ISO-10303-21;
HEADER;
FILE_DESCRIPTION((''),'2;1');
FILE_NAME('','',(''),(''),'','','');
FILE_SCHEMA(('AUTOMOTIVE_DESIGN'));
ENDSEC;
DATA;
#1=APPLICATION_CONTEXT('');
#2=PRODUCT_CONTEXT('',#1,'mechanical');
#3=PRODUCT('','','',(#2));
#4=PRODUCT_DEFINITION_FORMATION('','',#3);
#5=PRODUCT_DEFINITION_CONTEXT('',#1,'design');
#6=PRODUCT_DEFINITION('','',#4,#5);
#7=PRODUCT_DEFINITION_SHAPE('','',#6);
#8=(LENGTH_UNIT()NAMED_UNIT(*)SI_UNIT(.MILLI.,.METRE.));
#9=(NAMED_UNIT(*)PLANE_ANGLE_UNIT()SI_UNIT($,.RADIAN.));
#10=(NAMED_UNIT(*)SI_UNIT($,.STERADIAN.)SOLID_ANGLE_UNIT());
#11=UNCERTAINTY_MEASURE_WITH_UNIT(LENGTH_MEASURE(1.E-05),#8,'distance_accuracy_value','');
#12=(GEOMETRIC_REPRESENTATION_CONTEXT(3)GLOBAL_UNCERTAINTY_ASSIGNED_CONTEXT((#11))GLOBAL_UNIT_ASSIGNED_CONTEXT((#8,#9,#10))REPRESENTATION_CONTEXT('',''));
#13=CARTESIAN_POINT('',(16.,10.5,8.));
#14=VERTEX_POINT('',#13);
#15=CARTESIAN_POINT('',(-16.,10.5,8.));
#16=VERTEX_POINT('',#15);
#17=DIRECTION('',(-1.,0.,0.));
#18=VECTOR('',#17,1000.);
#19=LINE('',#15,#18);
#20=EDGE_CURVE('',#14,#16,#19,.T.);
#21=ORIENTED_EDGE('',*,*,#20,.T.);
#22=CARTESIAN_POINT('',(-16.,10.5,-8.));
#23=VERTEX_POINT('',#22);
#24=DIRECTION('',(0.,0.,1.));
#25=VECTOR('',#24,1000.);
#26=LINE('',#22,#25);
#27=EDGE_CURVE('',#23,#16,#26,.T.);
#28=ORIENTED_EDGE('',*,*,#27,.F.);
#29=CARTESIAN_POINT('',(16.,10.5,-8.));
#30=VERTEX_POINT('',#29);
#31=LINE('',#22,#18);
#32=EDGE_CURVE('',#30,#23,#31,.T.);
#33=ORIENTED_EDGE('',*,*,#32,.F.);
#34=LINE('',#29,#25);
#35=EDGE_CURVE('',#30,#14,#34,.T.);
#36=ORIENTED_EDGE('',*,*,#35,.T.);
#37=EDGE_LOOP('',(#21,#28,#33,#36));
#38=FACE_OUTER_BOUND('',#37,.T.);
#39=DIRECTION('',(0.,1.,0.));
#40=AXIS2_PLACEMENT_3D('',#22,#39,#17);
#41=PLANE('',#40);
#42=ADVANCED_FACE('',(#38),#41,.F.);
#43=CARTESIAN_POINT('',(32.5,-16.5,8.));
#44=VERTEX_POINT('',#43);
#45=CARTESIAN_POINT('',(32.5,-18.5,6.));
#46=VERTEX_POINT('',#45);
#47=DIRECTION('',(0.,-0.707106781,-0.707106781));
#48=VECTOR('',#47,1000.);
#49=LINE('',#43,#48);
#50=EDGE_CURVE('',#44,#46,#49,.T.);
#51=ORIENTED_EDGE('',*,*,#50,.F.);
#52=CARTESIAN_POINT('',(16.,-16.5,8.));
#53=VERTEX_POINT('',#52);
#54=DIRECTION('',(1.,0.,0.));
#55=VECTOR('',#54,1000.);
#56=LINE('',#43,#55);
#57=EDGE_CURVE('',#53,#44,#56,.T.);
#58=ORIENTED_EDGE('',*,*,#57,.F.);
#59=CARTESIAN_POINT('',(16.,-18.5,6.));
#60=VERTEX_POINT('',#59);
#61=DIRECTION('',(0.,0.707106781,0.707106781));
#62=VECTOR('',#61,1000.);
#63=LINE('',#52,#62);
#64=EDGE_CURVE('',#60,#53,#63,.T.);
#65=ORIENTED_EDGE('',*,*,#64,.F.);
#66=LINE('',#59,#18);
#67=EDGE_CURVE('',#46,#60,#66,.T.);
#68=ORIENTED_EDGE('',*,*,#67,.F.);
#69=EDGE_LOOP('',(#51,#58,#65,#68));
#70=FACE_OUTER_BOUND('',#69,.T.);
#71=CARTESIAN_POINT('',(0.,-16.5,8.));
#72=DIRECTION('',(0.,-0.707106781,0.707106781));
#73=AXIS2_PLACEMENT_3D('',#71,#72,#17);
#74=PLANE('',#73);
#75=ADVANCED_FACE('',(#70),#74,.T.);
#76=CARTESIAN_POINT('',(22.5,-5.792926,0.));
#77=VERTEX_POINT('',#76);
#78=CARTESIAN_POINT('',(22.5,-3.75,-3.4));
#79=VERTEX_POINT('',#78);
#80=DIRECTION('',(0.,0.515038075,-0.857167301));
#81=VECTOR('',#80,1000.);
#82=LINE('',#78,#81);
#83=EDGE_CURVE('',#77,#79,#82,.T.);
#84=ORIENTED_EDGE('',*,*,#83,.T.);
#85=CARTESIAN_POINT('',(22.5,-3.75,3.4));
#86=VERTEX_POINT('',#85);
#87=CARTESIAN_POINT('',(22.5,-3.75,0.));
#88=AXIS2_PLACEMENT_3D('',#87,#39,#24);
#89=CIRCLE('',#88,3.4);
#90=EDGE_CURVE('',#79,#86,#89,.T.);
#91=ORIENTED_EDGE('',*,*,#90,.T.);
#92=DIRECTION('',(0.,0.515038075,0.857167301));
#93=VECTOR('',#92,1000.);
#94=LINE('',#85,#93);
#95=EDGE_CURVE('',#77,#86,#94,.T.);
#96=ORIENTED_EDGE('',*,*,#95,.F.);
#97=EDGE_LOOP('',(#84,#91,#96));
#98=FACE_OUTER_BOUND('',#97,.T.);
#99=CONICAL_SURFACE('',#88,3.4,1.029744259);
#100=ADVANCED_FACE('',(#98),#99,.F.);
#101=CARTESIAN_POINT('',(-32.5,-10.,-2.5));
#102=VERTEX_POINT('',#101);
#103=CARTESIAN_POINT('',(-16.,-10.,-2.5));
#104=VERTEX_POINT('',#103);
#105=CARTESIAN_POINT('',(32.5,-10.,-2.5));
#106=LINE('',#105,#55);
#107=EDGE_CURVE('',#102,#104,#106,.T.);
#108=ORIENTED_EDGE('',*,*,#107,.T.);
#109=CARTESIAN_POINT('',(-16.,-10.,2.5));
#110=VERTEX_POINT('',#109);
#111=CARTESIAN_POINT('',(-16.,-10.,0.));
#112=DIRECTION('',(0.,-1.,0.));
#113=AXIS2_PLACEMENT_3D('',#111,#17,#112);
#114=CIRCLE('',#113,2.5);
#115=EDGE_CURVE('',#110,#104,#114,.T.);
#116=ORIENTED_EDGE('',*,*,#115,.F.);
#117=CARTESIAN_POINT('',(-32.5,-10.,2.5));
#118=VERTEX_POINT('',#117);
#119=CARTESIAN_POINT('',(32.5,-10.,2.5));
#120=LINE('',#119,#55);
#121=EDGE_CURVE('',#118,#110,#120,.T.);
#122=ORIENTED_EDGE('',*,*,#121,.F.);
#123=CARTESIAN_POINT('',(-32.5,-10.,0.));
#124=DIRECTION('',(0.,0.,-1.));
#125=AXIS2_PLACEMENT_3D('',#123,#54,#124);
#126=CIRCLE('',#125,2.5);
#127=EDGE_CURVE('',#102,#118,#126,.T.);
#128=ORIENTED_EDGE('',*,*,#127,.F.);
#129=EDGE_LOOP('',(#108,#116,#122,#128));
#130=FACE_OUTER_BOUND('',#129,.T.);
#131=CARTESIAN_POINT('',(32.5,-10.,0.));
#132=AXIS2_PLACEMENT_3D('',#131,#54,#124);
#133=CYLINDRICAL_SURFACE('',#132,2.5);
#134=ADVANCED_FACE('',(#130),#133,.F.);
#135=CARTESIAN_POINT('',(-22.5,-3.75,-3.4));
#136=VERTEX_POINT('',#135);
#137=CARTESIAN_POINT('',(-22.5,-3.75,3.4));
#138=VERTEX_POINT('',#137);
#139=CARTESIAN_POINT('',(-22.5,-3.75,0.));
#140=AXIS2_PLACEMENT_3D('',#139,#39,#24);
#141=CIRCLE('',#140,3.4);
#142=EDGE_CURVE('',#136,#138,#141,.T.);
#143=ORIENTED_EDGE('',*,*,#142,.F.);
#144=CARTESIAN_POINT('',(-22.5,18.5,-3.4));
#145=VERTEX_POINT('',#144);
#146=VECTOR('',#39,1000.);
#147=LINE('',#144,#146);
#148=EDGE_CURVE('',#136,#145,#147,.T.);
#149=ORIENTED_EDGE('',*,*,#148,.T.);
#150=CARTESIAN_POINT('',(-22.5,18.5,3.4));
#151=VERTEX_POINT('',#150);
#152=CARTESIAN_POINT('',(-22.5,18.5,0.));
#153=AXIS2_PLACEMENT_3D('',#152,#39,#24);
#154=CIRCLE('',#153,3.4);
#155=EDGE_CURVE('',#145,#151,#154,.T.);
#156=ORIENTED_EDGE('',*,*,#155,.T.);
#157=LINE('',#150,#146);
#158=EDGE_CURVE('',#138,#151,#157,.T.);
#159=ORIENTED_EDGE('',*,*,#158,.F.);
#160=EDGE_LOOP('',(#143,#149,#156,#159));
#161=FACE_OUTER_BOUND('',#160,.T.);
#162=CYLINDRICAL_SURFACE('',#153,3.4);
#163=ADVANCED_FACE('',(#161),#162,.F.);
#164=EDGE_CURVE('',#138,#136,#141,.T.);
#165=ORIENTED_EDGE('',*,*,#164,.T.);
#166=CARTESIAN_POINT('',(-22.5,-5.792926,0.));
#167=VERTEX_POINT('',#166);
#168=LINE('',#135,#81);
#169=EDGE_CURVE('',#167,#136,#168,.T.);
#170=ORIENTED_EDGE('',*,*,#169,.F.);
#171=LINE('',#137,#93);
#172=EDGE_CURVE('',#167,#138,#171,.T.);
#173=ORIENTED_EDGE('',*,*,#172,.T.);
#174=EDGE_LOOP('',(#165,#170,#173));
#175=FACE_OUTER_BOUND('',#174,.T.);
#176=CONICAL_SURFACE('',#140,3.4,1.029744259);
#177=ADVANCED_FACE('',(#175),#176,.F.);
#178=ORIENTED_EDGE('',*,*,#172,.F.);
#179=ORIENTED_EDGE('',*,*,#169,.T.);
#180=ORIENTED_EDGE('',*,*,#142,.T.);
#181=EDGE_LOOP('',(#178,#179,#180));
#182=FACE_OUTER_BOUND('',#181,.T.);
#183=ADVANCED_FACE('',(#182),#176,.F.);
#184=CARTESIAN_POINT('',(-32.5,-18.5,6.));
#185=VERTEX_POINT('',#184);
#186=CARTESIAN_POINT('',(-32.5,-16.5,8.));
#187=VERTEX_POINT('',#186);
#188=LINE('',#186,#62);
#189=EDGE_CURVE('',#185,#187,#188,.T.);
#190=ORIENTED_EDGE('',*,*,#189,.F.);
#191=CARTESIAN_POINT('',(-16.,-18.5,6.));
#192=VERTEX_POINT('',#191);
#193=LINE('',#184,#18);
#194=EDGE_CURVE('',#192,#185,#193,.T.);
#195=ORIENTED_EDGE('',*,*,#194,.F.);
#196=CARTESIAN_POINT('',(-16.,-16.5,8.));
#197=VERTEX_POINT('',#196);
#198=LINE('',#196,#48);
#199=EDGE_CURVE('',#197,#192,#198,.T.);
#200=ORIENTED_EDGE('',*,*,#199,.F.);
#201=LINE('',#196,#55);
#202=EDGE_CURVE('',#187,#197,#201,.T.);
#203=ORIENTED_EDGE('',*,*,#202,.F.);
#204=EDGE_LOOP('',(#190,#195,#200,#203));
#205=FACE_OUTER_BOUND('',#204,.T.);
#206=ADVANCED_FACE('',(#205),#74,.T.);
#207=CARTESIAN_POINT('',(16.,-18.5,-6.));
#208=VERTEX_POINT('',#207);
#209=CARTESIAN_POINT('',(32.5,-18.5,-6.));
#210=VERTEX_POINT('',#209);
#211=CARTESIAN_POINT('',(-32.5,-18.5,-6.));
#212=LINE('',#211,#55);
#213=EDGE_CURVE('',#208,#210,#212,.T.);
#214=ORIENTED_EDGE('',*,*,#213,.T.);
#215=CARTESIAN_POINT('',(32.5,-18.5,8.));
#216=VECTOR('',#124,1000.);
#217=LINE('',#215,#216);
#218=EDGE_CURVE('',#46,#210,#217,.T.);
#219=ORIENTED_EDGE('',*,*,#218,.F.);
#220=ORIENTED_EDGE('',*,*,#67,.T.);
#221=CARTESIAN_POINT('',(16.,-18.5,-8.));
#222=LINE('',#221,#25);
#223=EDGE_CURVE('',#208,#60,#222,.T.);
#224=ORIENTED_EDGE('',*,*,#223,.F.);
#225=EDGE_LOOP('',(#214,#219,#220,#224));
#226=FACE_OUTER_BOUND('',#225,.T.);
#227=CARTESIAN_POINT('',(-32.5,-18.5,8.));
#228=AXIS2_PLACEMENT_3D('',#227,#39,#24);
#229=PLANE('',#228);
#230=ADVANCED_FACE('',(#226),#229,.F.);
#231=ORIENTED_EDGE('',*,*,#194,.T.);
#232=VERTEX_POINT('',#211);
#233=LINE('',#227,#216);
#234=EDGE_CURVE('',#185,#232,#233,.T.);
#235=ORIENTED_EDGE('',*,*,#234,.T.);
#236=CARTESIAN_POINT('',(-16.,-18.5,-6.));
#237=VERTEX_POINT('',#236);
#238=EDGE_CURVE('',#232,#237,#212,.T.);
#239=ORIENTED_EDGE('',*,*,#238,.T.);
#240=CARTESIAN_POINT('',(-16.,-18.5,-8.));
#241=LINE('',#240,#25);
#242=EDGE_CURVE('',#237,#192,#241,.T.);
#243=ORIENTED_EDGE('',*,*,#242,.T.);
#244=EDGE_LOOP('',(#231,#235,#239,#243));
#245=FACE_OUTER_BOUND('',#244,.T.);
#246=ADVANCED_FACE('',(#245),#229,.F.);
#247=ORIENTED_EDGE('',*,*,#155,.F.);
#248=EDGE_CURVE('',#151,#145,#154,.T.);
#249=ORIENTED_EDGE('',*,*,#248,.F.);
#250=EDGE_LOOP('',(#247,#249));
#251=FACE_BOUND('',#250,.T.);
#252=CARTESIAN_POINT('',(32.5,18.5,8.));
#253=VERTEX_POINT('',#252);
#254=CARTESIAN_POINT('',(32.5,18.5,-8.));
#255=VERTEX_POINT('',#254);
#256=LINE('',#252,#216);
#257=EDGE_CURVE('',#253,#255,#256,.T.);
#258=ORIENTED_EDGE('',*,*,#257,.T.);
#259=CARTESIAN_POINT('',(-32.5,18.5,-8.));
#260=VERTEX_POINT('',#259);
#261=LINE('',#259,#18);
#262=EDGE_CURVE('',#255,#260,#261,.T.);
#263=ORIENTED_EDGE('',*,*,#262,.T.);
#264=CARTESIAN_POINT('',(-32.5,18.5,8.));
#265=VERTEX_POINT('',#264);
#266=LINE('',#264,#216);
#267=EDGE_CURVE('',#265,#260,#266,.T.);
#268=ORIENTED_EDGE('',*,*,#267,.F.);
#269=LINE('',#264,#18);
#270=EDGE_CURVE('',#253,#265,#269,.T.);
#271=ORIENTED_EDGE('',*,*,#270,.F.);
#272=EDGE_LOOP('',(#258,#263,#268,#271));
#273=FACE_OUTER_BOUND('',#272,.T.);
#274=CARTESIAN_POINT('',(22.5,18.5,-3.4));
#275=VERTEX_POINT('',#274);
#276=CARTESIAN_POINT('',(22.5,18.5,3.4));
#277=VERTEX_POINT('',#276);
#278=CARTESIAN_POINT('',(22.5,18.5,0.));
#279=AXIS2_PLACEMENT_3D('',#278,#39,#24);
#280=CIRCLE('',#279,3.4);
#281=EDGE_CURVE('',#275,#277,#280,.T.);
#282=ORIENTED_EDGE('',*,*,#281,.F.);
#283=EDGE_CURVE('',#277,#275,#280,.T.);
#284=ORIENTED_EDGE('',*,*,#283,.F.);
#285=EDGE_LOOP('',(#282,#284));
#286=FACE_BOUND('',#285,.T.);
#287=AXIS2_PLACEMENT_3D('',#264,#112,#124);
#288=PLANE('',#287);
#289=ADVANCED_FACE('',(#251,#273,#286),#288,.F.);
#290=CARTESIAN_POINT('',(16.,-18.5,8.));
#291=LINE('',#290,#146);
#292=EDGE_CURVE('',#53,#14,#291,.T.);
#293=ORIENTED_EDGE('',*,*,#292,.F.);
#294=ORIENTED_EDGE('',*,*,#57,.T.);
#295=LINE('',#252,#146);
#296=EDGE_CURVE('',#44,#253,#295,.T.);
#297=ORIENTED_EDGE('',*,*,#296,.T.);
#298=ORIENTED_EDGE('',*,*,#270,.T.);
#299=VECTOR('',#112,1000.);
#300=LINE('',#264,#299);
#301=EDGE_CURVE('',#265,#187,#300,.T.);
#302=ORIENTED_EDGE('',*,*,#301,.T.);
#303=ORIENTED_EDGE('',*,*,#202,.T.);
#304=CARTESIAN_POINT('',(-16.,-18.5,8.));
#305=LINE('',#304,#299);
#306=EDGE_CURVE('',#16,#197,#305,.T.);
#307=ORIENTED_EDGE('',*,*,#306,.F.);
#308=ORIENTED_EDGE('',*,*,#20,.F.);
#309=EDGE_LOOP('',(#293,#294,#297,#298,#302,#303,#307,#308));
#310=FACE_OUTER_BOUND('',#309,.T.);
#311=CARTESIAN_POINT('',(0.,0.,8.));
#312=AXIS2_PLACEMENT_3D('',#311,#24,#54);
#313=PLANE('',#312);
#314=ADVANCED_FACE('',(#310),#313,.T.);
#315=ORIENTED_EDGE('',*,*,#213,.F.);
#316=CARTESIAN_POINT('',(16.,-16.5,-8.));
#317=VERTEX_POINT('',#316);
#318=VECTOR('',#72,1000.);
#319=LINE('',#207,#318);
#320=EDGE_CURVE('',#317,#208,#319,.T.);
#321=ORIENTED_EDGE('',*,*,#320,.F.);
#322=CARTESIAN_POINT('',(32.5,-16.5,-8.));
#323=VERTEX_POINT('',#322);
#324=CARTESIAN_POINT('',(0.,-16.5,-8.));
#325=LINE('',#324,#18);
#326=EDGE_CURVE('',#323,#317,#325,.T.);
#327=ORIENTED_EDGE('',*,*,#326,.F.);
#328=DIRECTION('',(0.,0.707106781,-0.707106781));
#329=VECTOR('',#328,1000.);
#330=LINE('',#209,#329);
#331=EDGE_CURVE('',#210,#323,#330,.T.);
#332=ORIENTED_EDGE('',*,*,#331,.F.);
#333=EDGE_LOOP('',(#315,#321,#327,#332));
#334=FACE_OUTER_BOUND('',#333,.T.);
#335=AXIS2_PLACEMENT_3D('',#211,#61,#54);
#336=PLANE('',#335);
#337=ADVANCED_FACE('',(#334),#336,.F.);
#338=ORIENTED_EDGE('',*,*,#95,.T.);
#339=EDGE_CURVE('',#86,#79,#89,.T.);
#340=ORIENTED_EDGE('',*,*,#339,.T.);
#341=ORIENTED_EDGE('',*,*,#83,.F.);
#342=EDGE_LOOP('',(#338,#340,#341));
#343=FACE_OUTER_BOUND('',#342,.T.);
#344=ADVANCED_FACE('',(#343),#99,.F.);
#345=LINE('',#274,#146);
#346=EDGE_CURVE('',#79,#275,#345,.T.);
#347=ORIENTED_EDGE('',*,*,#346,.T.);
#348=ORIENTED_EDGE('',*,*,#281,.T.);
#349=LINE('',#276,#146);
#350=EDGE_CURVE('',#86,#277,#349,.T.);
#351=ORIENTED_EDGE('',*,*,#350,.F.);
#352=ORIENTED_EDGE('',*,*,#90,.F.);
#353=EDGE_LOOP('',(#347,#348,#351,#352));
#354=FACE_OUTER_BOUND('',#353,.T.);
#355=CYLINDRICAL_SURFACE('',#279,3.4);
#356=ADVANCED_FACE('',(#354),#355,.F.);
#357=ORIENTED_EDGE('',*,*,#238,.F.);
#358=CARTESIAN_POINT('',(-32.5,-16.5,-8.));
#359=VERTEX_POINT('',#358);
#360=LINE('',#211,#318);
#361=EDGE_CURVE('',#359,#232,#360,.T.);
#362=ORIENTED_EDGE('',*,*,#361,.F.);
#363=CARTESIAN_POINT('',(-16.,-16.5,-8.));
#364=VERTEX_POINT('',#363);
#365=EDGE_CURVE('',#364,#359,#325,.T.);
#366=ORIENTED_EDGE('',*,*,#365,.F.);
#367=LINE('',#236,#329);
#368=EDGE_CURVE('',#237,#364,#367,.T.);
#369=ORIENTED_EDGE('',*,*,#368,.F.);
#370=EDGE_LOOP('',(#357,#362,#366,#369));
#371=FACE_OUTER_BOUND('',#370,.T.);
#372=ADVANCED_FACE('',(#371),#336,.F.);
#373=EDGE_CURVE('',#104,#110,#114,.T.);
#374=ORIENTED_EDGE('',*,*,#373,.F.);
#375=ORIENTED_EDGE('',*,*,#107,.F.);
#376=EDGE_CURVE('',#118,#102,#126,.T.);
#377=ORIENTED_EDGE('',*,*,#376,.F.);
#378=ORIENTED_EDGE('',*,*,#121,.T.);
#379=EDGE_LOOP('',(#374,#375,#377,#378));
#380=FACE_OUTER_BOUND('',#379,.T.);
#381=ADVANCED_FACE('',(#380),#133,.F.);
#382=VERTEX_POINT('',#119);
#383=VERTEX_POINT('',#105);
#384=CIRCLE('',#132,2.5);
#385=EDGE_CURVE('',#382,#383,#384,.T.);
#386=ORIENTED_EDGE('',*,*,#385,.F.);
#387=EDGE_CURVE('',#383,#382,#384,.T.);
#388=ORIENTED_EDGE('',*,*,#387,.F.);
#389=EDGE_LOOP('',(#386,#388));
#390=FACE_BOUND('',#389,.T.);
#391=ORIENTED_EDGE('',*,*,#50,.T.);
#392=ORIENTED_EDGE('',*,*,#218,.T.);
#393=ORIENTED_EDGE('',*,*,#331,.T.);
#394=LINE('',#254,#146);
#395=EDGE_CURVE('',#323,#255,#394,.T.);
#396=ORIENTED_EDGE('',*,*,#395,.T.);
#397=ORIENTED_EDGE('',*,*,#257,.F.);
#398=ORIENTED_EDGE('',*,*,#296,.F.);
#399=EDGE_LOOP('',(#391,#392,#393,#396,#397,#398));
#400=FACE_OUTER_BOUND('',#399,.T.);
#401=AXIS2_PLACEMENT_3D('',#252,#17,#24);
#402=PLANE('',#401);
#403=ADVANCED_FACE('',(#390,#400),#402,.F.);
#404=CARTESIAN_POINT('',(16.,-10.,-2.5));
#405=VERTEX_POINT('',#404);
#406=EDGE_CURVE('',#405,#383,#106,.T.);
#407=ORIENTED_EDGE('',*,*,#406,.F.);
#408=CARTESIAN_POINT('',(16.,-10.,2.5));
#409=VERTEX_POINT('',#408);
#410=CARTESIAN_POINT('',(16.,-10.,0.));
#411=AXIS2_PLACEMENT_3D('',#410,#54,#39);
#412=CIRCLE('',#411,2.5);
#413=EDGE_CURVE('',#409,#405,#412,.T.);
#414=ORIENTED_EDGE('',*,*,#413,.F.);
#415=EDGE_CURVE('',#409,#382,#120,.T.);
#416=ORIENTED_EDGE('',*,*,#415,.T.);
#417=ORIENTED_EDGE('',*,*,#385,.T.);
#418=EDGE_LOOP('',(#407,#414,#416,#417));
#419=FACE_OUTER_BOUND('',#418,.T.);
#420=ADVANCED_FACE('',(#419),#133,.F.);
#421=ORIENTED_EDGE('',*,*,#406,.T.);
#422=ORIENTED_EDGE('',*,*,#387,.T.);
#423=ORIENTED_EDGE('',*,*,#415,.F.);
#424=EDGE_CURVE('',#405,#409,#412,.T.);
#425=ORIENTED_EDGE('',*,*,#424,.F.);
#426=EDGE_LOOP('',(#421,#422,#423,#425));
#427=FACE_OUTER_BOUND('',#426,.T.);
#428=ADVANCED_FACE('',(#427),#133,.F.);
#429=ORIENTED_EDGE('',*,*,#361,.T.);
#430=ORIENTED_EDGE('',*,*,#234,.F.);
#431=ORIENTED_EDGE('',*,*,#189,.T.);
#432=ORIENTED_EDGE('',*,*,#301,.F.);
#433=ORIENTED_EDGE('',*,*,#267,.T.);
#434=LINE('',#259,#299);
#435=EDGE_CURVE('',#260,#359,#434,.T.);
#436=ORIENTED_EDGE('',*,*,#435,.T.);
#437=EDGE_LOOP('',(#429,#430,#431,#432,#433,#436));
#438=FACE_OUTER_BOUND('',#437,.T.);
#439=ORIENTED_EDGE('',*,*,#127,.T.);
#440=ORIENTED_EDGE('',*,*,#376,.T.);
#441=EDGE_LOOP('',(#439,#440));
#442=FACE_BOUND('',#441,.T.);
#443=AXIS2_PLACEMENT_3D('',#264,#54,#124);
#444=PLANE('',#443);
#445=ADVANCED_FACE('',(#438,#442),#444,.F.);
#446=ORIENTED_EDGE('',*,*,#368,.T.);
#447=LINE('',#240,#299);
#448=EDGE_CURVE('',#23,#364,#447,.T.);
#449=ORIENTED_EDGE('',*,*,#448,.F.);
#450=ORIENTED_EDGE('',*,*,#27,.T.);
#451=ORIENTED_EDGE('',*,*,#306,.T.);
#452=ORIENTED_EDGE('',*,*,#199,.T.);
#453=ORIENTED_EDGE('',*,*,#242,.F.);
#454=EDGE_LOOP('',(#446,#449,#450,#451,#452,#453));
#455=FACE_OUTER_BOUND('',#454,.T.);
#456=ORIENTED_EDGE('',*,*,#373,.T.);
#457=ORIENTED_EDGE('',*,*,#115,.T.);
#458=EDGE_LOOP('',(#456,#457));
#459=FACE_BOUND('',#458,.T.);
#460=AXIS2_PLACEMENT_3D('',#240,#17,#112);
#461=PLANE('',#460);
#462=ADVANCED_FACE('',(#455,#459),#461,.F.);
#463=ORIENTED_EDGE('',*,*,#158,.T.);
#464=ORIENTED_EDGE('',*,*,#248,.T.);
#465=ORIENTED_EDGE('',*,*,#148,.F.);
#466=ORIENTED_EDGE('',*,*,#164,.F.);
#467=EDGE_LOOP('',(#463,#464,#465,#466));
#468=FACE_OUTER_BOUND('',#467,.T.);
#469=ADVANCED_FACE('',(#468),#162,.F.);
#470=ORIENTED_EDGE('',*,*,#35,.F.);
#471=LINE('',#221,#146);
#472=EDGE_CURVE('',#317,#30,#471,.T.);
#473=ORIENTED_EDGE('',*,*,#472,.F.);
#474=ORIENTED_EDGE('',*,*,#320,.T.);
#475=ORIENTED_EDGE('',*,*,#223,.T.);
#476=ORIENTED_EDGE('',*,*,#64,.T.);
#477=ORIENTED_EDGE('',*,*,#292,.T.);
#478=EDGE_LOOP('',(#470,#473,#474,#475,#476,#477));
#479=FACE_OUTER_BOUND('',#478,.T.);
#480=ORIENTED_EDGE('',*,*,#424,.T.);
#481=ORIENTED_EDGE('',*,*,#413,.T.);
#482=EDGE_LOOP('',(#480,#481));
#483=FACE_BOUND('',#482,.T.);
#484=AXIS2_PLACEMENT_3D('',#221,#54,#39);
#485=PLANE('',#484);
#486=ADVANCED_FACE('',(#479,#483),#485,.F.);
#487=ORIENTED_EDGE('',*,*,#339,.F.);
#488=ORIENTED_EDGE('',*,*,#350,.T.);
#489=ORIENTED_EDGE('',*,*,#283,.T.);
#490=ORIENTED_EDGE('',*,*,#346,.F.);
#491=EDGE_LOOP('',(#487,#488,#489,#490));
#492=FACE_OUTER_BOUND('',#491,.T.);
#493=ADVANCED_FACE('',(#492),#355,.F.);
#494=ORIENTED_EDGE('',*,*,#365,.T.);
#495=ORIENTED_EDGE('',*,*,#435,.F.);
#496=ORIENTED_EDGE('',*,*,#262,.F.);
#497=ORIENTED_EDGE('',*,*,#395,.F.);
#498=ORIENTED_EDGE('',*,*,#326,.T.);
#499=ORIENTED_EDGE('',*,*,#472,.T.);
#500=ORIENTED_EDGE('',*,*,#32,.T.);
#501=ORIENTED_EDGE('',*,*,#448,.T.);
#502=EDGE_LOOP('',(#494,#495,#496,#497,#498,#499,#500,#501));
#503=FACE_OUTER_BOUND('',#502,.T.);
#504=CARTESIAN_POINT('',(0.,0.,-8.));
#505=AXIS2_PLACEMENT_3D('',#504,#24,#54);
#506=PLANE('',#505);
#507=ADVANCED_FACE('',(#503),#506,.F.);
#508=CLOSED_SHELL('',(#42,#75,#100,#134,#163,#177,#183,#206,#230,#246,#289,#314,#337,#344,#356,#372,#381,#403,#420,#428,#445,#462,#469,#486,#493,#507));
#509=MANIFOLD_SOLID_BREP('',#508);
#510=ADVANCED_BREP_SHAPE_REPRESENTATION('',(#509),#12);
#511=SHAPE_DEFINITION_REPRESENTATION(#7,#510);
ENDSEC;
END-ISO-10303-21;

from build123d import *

# Parameters (mm, degrees)
SKETCH_1_W             = 65
SKETCH_1_H             = 37
EXTRUDE_1_DEPTH        = 8
SKETCH_3_W             = 32
SKETCH_3_H             = 29
CUT_EXTRUDE_1_DEPTH    = 41.675545479
HOLE_WIZARD_M6_1_D     = 5
HOLE_WIZARD_M8_2_D     = 6.8
HOLE_WIZARD_M8_2_DEPTH = 22.25
HOLE_WIZARD_M8_2_TIP   = 2.042926105
CHAMFER_1_SIZE         = 2


with BuildPart() as part:
    # 草图1 → 凸台-拉伸1 (new, symmetric)
    with BuildSketch(Plane.XY):
        Rectangle(SKETCH_1_W, SKETCH_1_H)
    extrude(amount=EXTRUDE_1_DEPTH, both=True)

    # 草图3 → 切除-拉伸1 (cut, through all)
    with BuildSketch(Plane.XY.offset(8)):
        with Locations((0, -4)):
            Rectangle(SKETCH_3_W, SKETCH_3_H)
    extrude(amount=-CUT_EXTRUDE_1_DEPTH, mode=Mode.SUBTRACT)

    # M6 螺纹孔1 (through all)
    with Locations(Plane(origin=(32.5, 0, 0), x_dir=(0, 0, -1), z_dir=(1, 0, 0))):
        with Locations((0, -10)):
            Hole(HOLE_WIZARD_M6_1_D / 2)

    # M8 螺纹孔2
    with Locations(Plane(origin=(0, 18.5, 0), x_dir=(1, 0, 0), z_dir=(0, 1, 0))):
        with Locations((-22.5, 0), (22.5, 0)):
            Hole(HOLE_WIZARD_M8_2_D / 2, depth=HOLE_WIZARD_M8_2_DEPTH)
            with Locations((0, 0, -(HOLE_WIZARD_M8_2_DEPTH + HOLE_WIZARD_M8_2_TIP / 2))):  # 118° drill point
                Cone(0, HOLE_WIZARD_M8_2_D / 2, HOLE_WIZARD_M8_2_TIP, mode=Mode.SUBTRACT)

    # 倒角1
    chamfer_1_edges = [part.edges().sort_by_distance(p)[0] for p in [
        (24.25, -18.5, -8),
        (24.25, -18.5, 8),
        (-24.25, -18.5, -8),
        (-24.25, -18.5, 8),
    ]]
    chamfer(chamfer_1_edges, length=CHAMFER_1_SIZE)


solid = part.part
